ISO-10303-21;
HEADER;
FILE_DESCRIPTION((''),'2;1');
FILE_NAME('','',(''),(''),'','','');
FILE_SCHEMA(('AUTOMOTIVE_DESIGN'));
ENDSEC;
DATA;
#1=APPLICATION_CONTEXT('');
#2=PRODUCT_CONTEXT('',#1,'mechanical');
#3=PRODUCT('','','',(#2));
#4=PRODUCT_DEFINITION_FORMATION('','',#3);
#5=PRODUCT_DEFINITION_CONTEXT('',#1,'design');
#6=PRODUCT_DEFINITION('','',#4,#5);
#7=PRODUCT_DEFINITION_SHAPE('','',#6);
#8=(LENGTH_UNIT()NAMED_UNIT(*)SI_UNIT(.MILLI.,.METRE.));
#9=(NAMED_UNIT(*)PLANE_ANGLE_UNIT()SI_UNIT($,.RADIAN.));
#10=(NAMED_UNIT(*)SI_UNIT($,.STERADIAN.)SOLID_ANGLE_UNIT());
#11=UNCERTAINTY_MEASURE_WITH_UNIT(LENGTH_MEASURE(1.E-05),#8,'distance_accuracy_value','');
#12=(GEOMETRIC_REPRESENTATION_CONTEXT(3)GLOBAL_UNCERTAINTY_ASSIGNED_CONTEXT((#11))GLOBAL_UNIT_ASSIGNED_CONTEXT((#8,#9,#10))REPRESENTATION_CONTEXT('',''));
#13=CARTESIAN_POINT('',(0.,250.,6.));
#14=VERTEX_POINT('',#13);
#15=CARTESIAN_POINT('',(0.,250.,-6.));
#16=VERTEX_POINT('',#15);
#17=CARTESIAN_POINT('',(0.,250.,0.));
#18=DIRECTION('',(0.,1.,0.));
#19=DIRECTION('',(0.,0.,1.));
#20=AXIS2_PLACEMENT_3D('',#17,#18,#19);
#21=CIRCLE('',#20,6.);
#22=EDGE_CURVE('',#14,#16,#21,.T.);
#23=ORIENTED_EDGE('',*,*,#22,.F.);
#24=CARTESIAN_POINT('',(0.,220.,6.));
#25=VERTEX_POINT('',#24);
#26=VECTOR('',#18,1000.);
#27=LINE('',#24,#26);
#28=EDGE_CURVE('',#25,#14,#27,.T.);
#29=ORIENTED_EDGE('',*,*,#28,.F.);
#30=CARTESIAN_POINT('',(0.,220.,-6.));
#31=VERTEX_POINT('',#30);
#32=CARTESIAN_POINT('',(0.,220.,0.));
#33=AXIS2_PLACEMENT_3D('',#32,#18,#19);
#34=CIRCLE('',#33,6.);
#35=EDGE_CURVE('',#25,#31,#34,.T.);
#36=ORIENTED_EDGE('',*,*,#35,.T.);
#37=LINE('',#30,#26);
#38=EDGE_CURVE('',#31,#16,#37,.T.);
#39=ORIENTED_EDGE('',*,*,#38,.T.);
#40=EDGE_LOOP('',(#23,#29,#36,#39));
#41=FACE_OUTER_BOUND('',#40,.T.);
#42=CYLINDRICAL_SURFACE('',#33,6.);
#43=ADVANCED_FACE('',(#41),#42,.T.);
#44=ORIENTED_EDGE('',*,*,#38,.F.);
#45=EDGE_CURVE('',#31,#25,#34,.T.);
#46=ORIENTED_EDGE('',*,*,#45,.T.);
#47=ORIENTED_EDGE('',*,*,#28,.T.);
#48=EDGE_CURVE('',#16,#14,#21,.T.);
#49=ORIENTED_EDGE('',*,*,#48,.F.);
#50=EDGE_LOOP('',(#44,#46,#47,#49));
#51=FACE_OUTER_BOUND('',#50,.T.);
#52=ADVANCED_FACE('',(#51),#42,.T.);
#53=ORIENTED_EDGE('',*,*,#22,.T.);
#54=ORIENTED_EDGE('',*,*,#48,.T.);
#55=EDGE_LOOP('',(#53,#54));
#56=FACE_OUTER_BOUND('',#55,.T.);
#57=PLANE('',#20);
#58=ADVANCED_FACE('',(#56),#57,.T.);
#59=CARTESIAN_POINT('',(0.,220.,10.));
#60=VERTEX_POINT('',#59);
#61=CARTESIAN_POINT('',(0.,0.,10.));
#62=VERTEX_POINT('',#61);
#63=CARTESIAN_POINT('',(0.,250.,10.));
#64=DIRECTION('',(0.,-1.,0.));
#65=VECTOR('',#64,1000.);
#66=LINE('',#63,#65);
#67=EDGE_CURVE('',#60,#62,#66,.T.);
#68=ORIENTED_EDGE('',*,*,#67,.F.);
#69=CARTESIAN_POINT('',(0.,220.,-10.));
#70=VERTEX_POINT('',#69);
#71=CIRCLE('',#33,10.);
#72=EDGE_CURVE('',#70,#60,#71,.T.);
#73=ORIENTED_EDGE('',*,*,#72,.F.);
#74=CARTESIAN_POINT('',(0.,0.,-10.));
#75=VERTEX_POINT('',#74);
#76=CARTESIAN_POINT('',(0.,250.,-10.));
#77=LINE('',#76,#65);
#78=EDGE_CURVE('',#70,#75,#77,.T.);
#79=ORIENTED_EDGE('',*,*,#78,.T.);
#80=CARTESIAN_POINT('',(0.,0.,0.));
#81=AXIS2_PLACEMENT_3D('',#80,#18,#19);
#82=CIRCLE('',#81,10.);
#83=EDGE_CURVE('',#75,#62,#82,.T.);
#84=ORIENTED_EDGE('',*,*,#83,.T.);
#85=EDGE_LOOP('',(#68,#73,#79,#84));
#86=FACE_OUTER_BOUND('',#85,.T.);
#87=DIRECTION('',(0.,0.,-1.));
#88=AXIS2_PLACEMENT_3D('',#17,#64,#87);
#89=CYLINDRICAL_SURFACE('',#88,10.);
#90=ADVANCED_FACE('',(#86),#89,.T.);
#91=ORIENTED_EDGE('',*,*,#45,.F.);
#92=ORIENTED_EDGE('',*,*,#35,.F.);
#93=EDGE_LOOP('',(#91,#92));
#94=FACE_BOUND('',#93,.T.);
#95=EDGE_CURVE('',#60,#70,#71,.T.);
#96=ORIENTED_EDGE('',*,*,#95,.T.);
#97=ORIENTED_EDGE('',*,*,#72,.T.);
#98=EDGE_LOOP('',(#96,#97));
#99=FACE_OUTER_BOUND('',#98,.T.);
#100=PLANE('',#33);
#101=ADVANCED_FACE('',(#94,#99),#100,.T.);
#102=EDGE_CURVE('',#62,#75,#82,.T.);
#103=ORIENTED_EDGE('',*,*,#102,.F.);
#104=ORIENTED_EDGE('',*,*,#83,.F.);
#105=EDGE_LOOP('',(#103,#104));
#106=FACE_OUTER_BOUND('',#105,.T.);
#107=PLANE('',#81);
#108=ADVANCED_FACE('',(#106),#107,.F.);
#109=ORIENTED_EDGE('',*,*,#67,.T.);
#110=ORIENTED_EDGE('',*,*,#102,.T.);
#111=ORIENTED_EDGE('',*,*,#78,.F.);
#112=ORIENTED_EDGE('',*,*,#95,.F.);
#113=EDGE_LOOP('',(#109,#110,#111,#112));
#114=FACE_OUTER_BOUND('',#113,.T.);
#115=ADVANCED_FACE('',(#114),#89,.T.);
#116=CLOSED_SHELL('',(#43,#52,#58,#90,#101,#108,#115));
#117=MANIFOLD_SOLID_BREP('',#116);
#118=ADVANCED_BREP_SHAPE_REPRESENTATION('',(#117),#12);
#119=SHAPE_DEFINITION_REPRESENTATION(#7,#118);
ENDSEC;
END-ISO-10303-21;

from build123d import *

# Parameters (mm, degrees)
SKETCH1_R           = 10
BOSS_EXTRUDE1_DEPTH = 250
SKETCH2_OUTSIDE_W   = 72.318
SKETCH2_OUTSIDE_H   = 72.318
SKETCH2_OUTSIDE_R   = 6
CUT_EXTRUDE1_DEPTH  = 30


with BuildPart() as part:
    # Sketch1 → Boss-Extrude1 (new body)
    with BuildSketch(Plane(origin=(0, 0, 0), x_dir=(1, 0, 0), z_dir=(0, 1, 0))):
        with Locations(Location((0, 0, 0), (0, 0, 270))):
            Circle(SKETCH1_R)
    extrude(amount=BOSS_EXTRUDE1_DEPTH)

    # Sketch2 outside → Cut-Extrude1 (cut)
    with BuildSketch(Plane(origin=(0, 250, 0), x_dir=(1, 0, 0), z_dir=(0, 1, 0))):
        Rectangle(SKETCH2_OUTSIDE_W, SKETCH2_OUTSIDE_H)
        with Locations(Location((0, 0, 0), (0, 0, 270))):
            Circle(SKETCH2_OUTSIDE_R, mode=Mode.SUBTRACT)
    extrude(amount=-CUT_EXTRUDE1_DEPTH, mode=Mode.SUBTRACT)


solid = part.part
